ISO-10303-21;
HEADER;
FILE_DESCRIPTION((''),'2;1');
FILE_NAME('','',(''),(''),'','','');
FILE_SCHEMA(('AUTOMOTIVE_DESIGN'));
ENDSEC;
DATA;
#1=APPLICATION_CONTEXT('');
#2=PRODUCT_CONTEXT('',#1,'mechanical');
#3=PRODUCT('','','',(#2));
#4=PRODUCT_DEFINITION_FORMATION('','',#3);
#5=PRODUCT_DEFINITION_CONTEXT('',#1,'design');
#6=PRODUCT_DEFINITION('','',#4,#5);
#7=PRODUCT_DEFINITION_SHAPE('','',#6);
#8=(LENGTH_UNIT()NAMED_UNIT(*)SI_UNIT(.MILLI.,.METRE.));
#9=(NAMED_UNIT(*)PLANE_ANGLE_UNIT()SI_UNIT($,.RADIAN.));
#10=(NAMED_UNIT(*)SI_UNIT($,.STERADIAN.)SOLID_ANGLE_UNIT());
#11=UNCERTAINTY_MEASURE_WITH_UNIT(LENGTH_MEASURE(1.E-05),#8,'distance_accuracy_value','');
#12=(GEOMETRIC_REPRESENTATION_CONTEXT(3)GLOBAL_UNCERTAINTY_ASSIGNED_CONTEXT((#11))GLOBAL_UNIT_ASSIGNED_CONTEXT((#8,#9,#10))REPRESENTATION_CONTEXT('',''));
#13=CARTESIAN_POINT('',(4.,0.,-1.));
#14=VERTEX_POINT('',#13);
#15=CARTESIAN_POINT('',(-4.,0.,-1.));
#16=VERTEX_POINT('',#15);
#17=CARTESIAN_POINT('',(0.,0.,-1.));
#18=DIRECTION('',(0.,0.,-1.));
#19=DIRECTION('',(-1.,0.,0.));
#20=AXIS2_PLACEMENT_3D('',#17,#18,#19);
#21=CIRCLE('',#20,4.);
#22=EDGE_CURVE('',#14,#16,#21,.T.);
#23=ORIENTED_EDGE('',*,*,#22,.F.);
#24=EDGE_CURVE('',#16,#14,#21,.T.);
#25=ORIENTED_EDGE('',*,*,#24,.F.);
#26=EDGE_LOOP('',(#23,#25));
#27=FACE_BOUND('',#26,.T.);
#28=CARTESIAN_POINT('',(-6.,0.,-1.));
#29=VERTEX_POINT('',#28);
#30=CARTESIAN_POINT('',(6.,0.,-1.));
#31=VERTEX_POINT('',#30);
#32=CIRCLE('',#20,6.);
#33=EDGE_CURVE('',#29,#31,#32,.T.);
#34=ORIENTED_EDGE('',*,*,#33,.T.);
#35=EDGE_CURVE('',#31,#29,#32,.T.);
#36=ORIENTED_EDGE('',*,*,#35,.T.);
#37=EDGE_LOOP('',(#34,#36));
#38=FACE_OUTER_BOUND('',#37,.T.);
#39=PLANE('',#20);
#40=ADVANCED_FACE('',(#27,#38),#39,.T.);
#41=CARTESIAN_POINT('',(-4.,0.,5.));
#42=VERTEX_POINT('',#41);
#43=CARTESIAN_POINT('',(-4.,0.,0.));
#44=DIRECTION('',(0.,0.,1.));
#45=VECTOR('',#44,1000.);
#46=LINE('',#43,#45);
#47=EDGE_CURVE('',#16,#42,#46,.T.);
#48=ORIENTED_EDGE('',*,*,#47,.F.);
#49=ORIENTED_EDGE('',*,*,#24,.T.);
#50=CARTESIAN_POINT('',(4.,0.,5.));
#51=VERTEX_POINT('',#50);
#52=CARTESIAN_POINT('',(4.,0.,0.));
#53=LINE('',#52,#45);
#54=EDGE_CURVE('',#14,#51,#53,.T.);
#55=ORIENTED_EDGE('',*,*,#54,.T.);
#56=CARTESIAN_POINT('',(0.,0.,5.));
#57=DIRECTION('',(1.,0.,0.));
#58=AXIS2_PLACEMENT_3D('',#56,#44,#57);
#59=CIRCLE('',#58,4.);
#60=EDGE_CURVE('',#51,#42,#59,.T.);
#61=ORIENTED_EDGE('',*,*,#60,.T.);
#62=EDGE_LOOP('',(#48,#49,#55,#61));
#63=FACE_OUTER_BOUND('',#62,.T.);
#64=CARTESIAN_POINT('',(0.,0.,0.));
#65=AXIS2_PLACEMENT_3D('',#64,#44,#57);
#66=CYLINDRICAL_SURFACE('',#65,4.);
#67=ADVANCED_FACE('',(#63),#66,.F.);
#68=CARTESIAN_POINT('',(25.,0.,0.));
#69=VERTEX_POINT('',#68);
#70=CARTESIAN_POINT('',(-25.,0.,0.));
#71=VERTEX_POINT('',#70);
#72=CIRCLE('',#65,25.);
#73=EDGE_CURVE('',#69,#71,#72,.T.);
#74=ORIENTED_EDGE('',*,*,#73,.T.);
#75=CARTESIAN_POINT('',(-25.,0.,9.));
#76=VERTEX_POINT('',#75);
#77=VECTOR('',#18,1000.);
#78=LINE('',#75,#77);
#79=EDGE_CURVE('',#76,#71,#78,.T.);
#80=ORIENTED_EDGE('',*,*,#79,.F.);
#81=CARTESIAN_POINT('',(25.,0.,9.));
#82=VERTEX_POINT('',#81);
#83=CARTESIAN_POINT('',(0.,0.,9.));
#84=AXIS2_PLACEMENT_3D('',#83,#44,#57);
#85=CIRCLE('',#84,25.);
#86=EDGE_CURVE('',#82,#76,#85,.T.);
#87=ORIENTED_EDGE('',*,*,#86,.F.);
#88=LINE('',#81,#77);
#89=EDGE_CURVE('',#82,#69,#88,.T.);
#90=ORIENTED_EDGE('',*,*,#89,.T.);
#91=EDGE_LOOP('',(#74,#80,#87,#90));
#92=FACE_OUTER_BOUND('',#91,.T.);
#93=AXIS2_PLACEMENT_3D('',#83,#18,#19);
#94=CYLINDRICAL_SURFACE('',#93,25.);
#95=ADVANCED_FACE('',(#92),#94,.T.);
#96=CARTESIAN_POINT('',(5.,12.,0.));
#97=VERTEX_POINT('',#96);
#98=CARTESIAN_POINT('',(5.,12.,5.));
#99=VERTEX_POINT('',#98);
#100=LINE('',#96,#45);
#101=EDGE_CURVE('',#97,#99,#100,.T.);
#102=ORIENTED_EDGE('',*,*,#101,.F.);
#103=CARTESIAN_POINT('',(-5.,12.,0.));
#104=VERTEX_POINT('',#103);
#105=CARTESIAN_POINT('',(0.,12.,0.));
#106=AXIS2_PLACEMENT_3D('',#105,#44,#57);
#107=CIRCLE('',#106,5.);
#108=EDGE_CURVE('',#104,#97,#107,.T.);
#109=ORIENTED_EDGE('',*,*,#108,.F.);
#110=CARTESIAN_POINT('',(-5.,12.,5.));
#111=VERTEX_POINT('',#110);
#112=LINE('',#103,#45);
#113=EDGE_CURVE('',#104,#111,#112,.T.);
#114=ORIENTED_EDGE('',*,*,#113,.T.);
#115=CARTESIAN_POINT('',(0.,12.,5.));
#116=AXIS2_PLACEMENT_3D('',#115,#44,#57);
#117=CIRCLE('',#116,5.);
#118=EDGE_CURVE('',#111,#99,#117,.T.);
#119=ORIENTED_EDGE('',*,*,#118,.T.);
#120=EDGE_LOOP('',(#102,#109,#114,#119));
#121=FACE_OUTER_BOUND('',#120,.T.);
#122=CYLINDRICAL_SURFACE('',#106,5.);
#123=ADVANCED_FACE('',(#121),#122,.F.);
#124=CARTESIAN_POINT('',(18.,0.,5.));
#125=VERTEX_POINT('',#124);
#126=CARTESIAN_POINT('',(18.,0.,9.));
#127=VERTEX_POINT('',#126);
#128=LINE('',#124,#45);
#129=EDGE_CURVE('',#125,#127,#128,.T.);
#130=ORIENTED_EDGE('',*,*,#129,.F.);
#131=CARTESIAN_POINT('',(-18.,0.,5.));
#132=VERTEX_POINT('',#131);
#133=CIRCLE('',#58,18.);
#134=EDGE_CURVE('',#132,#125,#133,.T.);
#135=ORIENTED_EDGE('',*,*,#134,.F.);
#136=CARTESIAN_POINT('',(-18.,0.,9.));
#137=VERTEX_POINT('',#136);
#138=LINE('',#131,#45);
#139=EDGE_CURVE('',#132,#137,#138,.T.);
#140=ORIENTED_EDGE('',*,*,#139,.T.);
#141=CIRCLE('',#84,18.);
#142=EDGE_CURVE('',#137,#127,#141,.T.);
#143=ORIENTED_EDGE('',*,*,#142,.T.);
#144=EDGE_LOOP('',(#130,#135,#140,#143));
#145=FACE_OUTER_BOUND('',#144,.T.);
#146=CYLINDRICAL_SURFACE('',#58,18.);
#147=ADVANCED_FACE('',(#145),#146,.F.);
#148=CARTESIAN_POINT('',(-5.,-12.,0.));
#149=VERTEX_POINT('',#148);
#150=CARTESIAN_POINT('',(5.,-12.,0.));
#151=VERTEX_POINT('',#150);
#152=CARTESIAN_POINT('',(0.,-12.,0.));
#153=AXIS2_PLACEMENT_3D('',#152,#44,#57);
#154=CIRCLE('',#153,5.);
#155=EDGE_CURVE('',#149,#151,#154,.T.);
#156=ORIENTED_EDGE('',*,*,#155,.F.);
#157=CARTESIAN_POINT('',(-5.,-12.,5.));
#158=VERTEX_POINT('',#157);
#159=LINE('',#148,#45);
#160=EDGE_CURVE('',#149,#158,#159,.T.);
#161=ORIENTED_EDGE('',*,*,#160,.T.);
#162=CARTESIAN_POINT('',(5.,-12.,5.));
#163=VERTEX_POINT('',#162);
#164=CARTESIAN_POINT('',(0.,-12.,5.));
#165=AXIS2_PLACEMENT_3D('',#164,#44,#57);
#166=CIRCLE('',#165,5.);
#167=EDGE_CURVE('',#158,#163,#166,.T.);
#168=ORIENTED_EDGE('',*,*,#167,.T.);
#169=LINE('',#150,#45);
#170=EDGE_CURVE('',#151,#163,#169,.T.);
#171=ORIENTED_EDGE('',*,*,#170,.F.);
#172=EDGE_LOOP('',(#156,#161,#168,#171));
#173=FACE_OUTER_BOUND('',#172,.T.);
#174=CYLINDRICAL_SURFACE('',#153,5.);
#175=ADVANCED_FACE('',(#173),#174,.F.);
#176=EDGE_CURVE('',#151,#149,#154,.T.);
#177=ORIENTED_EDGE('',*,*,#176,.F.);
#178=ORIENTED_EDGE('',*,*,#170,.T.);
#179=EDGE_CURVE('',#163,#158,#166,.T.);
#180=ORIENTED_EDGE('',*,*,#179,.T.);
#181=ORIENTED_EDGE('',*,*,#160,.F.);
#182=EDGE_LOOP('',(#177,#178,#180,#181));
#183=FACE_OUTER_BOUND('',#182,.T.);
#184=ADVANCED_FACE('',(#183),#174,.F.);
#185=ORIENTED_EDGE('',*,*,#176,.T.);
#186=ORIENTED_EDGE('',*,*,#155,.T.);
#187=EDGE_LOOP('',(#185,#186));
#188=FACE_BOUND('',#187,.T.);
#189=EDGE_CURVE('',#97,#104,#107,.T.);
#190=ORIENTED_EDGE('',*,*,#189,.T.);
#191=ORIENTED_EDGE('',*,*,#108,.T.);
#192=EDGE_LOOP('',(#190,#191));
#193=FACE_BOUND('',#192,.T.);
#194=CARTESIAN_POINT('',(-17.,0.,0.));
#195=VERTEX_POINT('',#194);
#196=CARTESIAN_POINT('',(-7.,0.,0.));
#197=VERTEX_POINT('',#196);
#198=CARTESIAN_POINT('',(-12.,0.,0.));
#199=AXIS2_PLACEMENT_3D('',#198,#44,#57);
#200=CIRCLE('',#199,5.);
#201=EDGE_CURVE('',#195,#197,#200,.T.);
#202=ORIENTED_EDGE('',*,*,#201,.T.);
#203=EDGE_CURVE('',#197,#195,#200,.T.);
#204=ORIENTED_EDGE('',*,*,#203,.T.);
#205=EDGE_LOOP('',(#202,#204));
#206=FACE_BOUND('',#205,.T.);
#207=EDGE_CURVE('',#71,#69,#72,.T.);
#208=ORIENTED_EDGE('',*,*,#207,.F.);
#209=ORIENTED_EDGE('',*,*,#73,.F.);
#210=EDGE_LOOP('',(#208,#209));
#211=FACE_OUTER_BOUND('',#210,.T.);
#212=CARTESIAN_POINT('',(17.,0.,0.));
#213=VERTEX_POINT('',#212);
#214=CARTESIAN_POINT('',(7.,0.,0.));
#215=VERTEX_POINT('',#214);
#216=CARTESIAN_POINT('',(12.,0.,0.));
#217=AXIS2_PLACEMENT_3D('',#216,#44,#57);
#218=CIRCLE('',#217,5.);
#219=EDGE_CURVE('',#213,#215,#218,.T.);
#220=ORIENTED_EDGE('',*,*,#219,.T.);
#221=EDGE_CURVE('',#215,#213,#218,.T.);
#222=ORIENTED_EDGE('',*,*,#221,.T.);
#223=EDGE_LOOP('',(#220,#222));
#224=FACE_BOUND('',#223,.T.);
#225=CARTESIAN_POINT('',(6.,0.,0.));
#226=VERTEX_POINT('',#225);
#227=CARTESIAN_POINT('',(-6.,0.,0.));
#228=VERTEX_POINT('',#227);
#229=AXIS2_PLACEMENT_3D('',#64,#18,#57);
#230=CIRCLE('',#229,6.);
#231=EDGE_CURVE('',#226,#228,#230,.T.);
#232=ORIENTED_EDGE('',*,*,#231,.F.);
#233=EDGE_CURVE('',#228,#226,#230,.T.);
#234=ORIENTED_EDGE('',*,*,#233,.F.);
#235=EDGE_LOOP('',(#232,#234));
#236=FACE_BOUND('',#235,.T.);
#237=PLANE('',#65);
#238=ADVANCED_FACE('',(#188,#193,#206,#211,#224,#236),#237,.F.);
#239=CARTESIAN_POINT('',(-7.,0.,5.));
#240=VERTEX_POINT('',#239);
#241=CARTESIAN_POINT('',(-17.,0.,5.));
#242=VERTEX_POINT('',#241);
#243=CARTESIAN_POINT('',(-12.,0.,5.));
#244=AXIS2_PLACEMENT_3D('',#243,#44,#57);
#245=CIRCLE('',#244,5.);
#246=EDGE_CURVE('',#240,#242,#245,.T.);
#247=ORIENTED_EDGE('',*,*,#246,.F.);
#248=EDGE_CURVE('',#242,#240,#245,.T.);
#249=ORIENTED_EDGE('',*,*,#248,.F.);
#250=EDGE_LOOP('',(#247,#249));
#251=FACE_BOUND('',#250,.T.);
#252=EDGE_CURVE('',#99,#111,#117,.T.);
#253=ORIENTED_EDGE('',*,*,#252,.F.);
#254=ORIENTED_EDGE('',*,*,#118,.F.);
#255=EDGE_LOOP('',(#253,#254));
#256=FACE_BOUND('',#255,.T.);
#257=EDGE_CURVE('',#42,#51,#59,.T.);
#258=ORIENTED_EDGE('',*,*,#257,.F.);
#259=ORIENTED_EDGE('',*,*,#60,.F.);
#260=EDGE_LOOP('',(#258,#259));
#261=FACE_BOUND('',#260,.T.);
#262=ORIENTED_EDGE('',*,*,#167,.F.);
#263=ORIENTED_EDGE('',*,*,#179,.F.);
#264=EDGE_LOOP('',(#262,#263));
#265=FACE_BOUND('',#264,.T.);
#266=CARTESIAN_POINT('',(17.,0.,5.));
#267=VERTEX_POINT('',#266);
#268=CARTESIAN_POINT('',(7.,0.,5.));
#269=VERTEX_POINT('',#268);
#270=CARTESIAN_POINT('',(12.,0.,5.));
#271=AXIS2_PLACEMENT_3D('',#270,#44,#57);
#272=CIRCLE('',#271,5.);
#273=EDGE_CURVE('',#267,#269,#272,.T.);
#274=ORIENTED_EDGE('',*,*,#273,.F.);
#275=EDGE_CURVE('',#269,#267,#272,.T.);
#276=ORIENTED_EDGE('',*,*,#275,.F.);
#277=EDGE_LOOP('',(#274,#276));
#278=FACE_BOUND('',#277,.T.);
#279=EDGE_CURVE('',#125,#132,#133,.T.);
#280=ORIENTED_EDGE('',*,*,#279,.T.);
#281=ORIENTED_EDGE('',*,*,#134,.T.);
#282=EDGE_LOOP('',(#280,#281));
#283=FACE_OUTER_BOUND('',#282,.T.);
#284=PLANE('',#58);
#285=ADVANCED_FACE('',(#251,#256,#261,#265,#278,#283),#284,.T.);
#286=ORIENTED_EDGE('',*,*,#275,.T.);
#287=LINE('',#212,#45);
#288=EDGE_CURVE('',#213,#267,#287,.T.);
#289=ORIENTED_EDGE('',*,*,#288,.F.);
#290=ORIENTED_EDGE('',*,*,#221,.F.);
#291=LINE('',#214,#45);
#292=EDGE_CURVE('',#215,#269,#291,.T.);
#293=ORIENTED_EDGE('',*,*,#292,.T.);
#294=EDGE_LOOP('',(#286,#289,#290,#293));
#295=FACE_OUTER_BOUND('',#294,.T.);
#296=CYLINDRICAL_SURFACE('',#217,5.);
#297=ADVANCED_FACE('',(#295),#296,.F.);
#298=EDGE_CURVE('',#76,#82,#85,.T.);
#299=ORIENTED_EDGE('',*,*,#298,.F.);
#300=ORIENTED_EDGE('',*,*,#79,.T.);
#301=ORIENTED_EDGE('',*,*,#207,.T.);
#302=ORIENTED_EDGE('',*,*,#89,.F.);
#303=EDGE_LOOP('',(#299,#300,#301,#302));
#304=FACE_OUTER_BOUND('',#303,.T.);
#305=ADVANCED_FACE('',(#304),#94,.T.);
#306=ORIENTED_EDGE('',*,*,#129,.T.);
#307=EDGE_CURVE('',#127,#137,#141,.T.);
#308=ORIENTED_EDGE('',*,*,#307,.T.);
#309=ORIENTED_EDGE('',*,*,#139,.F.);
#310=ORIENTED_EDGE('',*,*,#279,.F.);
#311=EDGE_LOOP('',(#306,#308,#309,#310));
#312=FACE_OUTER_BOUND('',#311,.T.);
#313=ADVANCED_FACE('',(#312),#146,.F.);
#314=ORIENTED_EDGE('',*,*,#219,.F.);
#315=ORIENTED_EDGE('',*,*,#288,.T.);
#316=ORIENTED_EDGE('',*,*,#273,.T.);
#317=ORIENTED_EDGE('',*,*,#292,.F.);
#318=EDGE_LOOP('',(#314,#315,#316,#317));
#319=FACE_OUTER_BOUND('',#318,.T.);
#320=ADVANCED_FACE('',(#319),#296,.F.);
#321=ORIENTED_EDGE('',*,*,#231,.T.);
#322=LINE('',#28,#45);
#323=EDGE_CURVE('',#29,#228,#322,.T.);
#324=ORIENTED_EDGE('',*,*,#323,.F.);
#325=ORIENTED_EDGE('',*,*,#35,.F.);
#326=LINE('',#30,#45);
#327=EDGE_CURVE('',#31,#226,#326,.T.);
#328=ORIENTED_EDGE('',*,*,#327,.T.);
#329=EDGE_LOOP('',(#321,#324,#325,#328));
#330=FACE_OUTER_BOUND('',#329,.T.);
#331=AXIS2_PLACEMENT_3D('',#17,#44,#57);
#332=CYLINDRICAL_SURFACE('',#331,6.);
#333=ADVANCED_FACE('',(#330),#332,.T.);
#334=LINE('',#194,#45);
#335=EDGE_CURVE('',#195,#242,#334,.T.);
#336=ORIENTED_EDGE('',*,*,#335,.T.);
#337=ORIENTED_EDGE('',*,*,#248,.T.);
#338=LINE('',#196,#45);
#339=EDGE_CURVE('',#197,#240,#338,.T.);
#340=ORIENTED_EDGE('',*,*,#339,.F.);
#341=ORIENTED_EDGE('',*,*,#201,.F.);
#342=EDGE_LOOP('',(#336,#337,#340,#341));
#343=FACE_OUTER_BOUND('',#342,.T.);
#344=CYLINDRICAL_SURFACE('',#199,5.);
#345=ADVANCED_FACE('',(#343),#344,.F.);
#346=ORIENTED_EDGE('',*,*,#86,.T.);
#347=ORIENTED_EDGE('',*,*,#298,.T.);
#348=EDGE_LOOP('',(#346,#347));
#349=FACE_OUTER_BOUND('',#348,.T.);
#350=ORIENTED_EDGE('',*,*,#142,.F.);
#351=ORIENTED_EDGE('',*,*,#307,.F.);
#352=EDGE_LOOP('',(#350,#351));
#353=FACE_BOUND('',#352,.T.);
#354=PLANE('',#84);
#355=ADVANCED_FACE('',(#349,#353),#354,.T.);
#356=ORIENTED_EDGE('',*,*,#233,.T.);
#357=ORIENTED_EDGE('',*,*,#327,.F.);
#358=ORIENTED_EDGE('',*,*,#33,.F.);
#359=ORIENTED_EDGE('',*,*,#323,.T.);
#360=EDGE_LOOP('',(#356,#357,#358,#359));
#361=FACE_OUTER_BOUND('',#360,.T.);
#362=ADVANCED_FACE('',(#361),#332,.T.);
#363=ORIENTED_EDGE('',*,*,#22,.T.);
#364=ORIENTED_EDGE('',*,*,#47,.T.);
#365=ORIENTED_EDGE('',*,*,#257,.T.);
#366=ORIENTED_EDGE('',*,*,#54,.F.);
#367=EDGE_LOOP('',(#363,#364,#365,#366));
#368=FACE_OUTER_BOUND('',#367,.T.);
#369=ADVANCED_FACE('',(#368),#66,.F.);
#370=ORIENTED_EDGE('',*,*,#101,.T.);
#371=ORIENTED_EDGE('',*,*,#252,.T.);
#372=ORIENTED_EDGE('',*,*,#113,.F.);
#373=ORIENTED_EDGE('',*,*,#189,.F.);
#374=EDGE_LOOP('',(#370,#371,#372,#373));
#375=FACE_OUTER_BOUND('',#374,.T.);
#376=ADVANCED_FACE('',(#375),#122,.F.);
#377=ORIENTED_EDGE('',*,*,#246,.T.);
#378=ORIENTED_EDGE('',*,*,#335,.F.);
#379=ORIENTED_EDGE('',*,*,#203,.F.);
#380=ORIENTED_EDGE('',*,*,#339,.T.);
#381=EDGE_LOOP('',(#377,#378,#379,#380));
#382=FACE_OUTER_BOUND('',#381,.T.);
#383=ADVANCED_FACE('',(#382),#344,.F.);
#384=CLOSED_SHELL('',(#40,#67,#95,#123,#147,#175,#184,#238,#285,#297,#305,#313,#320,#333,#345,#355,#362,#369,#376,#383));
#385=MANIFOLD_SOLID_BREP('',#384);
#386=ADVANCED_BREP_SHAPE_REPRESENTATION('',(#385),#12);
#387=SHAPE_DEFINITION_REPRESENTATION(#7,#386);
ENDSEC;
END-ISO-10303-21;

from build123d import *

# Parameters (mm, degrees)
SKETCH1_R           = 25
BOSS_EXTRUDE1_DEPTH = 9
SKETCH2_R           = 18
CUT_EXTRUDE1_DEPTH  = 4
SKETCH3_R           = 5
CUT_EXTRUDE2_DEPTH  = 36.707142143
SKETCH4_R           = 4
CUT_EXTRUDE3_DEPTH  = 36.707142143
SKETCH5_R           = 6
SKETCH5_R_2         = 4
BOSS_EXTRUDE2_DEPTH = 1


with BuildPart() as part:
    # Sketch1 → Boss-Extrude1 (new body)
    with BuildSketch(Plane.XY):
        Circle(SKETCH1_R)
    extrude(amount=BOSS_EXTRUDE1_DEPTH)

    # Sketch2 → Cut-Extrude1 (cut)
    with BuildSketch(Plane.XY.offset(9)):
        Circle(SKETCH2_R)
    extrude(amount=-CUT_EXTRUDE1_DEPTH, mode=Mode.SUBTRACT)

    # Sketch3 → Cut-Extrude2 (cut, through all)
    with BuildSketch(Plane.XY.offset(5)):
        with Locations((0, 12)):
            Circle(SKETCH3_R)
        with Locations((12, 0)):
            Circle(SKETCH3_R)
        with Locations((0, -12)):
            Circle(SKETCH3_R)
        with Locations((-12, 0)):
            Circle(SKETCH3_R)
    extrude(amount=-CUT_EXTRUDE2_DEPTH, mode=Mode.SUBTRACT)

    # Sketch4 → Cut-Extrude3 (cut, through all)
    with BuildSketch(Plane.XY.offset(5)):
        Circle(SKETCH4_R)
    extrude(amount=-CUT_EXTRUDE3_DEPTH, mode=Mode.SUBTRACT)

    # Sketch5 → Boss-Extrude2 (add)
    with BuildSketch(Plane(origin=(0, 0, 0), x_dir=(-1, 0, 0), z_dir=(0, 0, -1))):
        with Locations(Location((0, 0, 0), (0, 0, 180))):
            Circle(SKETCH5_R)
        with Locations(Location((0, 0, 0), (0, 0, 180))):
            Circle(SKETCH5_R_2, mode=Mode.SUBTRACT)
    extrude(amount=BOSS_EXTRUDE2_DEPTH)


solid = part.part
